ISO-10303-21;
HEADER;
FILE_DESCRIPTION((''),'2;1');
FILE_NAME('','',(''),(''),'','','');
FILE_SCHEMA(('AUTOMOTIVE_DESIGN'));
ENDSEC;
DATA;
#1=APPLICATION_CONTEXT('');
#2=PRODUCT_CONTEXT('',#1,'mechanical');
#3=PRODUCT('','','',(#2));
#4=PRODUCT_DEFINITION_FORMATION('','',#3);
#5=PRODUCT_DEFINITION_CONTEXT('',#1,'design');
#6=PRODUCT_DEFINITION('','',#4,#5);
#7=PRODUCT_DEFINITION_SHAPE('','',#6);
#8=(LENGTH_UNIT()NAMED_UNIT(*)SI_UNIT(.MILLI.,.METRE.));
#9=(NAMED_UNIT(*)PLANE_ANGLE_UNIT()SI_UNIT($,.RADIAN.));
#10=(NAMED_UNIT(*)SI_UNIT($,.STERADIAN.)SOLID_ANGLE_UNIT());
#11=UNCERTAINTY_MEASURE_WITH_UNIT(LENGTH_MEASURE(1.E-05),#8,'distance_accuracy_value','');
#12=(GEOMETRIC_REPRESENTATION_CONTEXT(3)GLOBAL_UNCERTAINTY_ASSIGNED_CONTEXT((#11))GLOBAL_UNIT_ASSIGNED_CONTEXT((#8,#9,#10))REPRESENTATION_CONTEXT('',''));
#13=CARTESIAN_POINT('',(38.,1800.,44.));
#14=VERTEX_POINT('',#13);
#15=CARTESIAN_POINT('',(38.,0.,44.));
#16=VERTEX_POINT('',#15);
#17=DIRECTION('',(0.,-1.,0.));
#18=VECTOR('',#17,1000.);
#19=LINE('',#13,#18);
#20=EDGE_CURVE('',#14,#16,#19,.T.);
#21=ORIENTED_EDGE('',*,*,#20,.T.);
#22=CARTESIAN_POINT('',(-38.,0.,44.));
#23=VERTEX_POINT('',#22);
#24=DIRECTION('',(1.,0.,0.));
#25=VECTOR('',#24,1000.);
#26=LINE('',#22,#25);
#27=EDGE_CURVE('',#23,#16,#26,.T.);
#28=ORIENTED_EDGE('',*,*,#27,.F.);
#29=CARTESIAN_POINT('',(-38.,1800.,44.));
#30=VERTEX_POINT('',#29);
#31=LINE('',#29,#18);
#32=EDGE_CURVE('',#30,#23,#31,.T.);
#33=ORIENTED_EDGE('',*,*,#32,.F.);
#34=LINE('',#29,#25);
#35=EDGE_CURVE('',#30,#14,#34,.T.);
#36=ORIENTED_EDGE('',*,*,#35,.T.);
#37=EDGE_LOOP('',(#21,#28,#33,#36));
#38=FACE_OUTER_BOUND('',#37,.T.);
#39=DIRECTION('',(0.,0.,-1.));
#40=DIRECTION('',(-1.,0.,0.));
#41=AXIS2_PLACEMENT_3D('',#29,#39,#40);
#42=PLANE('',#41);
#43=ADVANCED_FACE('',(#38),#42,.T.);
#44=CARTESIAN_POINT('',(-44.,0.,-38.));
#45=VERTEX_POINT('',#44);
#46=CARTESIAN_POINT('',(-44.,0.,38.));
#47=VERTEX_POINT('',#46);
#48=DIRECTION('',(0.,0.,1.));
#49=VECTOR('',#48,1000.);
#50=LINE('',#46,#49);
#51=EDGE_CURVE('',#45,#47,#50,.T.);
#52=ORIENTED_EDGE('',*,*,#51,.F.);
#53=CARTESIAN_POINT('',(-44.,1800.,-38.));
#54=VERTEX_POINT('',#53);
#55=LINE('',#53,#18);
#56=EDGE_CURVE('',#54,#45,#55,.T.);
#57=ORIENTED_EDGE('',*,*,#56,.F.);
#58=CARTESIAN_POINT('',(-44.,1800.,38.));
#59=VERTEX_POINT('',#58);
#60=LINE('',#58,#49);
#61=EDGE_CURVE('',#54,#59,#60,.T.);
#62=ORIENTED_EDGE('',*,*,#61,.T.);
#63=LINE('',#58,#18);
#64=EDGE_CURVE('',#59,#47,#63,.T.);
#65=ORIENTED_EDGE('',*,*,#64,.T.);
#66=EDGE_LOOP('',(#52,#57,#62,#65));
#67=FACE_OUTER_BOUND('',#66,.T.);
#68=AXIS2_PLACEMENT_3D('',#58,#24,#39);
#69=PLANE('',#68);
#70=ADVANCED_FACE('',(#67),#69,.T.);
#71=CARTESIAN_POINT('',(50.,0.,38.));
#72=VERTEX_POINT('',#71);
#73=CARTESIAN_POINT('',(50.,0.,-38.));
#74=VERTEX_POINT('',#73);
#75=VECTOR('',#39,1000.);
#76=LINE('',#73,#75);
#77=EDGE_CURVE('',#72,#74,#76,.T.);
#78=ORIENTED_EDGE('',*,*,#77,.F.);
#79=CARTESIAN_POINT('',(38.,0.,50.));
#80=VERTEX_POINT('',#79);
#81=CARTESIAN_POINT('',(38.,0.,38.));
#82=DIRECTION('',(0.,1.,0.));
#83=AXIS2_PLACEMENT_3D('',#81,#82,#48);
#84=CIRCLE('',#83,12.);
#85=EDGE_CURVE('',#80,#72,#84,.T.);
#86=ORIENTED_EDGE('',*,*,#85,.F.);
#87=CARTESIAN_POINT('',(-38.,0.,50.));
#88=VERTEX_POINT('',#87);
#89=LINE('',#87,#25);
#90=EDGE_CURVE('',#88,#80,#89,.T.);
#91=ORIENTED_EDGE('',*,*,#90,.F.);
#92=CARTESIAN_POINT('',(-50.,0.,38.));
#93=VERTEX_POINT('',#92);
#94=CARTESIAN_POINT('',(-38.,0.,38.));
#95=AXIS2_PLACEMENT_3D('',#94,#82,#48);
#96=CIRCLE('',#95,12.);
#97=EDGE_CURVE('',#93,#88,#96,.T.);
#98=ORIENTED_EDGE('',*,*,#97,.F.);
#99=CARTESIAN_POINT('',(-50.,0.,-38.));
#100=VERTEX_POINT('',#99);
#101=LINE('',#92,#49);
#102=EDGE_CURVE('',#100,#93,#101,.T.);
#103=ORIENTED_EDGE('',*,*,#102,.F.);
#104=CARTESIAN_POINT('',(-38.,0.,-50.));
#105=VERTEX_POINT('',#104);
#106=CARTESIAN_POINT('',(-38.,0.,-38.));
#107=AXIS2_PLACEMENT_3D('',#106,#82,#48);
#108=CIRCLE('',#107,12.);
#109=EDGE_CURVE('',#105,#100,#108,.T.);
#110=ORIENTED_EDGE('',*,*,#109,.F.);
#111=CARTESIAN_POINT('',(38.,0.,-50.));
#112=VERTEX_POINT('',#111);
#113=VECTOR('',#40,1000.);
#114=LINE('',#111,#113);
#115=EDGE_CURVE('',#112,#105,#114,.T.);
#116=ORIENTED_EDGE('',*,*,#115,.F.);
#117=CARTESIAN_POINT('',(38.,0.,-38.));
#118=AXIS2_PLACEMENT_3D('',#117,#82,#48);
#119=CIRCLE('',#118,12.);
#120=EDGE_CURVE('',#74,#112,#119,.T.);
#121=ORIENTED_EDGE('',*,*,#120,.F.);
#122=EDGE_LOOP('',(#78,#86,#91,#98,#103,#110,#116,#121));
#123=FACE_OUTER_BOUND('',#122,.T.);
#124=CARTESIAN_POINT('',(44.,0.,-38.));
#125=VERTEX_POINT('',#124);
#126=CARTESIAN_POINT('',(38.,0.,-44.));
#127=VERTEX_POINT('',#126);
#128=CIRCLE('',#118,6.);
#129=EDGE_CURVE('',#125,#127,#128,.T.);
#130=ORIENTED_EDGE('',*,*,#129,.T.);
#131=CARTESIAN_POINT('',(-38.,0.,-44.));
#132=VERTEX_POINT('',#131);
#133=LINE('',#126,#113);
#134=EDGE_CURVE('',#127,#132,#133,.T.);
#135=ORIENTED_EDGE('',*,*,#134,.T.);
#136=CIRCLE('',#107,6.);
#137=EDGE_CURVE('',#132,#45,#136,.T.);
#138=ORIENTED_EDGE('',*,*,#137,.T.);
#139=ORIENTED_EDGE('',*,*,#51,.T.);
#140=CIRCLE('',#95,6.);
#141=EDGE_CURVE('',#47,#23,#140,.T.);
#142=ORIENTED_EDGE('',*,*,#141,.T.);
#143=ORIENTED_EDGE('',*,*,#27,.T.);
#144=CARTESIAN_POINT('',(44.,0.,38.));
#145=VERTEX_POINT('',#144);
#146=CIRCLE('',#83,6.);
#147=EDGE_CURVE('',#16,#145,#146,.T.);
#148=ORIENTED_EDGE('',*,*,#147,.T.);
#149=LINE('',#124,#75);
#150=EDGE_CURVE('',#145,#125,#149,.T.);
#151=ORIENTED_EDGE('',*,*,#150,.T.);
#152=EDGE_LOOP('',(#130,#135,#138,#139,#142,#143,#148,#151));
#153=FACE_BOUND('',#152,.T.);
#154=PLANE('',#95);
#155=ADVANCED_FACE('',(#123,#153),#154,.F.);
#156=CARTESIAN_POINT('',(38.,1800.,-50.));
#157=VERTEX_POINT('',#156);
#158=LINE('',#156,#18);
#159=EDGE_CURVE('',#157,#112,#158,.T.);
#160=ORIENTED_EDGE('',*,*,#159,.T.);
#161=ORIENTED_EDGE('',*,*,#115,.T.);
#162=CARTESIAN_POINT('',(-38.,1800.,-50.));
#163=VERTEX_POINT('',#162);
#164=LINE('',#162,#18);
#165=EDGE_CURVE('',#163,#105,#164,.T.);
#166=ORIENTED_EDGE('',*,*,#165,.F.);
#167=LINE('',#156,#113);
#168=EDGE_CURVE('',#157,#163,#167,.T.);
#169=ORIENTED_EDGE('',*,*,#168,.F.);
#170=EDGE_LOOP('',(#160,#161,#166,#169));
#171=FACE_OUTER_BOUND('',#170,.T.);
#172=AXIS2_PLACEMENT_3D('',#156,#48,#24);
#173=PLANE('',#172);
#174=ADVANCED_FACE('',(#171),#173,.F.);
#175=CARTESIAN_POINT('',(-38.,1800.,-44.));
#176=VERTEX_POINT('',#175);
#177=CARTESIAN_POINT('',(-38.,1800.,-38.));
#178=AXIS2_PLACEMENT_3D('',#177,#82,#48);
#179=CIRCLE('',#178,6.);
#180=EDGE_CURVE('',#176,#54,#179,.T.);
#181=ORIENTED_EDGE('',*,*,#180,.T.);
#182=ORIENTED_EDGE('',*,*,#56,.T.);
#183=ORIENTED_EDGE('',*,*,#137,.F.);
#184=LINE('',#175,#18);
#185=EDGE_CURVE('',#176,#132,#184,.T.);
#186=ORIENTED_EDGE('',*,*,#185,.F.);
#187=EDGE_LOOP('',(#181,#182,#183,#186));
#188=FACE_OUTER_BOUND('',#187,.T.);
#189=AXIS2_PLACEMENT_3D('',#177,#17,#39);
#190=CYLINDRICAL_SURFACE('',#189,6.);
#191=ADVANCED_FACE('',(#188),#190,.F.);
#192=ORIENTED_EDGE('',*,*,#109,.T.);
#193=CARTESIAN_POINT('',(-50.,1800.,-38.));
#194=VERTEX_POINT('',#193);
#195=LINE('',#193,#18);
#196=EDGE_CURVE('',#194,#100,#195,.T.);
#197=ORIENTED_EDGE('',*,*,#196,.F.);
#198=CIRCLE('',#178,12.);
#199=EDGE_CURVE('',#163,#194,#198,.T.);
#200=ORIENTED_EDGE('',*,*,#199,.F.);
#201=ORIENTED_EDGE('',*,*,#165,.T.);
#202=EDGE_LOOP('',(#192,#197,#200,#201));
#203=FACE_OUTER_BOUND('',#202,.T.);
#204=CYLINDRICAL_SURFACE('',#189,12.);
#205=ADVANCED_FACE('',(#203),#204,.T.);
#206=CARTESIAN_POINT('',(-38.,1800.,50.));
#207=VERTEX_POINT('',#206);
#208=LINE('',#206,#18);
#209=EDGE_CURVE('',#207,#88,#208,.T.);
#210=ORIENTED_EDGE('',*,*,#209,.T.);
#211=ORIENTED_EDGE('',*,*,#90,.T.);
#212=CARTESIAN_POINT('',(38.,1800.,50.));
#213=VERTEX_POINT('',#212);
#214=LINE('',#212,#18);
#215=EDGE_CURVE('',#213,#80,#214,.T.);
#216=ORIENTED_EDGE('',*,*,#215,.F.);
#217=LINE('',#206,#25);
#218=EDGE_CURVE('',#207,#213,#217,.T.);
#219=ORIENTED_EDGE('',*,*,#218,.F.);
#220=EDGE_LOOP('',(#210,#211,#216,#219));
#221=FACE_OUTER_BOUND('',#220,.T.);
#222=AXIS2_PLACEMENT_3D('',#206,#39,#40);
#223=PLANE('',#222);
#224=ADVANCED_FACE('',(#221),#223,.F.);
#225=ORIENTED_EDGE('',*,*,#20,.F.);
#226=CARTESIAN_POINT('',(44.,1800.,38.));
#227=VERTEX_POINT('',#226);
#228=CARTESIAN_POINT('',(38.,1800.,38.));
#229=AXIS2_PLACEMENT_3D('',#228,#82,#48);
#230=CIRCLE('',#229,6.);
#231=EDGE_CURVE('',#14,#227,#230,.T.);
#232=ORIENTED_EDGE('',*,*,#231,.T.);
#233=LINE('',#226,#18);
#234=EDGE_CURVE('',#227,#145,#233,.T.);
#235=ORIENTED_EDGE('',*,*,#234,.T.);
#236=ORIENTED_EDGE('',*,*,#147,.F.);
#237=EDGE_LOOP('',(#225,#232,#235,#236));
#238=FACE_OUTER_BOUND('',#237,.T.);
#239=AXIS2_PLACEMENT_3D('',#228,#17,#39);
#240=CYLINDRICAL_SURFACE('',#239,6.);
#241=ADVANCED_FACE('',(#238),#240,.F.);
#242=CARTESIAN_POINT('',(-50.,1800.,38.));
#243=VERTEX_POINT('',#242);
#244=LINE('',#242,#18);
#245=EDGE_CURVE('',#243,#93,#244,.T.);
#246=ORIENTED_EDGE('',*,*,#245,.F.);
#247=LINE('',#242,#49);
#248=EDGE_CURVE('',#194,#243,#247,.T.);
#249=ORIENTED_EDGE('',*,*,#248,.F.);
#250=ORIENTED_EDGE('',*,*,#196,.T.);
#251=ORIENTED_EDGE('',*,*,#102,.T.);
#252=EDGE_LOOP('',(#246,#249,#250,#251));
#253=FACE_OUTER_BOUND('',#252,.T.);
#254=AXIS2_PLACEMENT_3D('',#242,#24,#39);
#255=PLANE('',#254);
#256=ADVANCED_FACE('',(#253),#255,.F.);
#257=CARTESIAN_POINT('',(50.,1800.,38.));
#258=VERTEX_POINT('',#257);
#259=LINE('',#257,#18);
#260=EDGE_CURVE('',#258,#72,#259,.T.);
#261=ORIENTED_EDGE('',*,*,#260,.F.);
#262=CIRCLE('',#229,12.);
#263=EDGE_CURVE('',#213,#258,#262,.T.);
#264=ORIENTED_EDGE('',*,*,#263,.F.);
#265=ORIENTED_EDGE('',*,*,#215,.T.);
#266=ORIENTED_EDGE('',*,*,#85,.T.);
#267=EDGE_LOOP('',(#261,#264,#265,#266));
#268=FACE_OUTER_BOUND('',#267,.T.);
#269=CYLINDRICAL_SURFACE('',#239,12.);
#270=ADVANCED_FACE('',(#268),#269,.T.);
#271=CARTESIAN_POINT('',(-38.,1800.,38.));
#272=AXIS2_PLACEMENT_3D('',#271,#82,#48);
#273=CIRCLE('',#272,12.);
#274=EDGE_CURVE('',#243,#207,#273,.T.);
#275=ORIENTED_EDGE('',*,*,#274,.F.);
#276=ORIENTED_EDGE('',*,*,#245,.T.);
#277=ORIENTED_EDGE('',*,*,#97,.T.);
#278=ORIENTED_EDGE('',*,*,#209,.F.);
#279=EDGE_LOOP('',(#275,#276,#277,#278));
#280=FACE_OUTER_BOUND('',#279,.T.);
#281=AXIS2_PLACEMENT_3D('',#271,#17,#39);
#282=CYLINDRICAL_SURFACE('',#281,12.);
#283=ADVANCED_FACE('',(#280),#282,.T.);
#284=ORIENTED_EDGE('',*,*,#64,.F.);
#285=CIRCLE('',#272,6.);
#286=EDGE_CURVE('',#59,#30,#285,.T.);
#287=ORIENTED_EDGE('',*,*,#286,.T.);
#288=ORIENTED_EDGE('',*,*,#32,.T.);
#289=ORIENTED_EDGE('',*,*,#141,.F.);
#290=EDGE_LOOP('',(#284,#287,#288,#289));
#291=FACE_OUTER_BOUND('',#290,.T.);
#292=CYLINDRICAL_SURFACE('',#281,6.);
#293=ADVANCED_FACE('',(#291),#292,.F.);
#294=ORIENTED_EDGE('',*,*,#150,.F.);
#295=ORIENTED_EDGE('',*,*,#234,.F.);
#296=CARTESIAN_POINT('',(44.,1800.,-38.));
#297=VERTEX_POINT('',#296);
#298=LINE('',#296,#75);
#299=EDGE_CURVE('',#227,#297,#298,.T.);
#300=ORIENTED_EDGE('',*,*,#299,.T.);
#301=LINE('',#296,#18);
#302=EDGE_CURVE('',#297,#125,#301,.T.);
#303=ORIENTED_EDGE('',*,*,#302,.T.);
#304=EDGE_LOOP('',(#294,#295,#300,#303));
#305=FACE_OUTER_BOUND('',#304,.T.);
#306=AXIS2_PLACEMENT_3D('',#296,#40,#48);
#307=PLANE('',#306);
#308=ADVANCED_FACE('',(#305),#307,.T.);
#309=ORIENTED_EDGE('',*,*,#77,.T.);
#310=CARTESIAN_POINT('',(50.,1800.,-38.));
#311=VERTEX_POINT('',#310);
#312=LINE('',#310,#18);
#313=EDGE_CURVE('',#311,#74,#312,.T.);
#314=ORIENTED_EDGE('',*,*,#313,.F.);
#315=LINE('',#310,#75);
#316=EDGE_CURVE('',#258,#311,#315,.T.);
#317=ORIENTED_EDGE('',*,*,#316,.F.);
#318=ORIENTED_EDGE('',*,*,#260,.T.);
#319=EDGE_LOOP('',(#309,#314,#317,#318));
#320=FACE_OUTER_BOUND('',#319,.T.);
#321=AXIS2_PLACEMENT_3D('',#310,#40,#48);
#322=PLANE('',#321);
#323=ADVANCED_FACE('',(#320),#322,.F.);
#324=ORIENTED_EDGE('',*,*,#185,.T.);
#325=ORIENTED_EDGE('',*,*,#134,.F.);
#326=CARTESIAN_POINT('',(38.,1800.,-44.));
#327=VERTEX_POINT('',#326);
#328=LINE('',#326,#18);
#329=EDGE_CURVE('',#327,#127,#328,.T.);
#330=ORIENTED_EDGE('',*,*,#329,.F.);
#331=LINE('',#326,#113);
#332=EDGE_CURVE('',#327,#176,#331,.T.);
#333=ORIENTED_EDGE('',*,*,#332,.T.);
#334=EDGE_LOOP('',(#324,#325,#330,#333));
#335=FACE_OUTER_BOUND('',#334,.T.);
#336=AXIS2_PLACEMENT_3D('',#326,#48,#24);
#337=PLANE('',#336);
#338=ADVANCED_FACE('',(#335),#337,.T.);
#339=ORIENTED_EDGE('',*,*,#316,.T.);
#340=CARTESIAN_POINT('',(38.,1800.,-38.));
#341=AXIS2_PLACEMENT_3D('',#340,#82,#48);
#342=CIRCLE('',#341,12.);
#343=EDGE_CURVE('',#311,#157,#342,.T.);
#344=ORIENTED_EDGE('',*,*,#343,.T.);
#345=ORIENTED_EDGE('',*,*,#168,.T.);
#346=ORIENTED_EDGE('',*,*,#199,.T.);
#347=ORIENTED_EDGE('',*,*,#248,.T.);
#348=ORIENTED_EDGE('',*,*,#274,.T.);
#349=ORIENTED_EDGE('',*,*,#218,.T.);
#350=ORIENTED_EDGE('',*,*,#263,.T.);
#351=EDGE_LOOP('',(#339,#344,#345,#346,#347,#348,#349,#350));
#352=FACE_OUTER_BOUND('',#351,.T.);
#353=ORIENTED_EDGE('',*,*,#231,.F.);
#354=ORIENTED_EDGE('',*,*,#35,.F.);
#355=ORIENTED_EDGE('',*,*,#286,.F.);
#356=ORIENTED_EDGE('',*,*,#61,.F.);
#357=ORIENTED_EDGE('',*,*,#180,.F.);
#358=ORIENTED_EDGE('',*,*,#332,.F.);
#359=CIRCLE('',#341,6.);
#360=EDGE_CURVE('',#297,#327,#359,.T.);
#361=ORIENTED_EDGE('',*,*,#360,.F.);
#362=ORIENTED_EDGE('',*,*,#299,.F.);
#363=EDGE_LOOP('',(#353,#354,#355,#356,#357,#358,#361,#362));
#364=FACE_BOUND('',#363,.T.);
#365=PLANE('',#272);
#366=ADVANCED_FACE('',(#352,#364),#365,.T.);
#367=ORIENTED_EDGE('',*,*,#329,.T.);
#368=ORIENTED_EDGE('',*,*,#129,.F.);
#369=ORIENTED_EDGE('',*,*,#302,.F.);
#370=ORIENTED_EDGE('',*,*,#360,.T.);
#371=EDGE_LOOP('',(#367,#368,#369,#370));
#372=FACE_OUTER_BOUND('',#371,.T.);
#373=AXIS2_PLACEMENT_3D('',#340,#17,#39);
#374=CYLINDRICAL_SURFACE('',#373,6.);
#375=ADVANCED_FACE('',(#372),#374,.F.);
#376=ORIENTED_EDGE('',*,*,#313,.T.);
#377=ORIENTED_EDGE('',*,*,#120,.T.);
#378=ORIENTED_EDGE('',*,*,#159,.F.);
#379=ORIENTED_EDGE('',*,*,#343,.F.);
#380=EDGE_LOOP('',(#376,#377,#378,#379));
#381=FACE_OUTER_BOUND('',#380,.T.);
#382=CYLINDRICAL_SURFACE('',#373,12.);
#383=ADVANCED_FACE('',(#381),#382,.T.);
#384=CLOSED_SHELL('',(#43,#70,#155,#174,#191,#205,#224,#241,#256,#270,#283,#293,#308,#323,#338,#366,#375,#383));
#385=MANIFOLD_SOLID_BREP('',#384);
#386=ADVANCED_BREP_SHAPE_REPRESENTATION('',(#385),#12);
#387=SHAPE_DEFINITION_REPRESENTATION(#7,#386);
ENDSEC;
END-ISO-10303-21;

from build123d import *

# Parameters (mm, degrees)
GB_T_6728_2002_SQUARE_HOLLOW_SECTION_100_DEPTH = 1800


with BuildPart() as part:
    # Sketch11 → GB/T 6728-2002 square hollow section 100×100×6(1) (new body)
    with BuildSketch(Plane(origin=(0, 0, 0), x_dir=(-1, 0, 0), z_dir=(0, 1, 0))):
        with BuildLine():
            Line((-38, -50), (38, -50))
            ThreePointArc((38, -50), (46.485281374, -46.485281374), (50, -38))
            Line((50, -38), (50, 38))
            ThreePointArc((50, 38), (46.485281374, 46.485281374), (38, 50))
            Line((38, 50), (-38, 50))
            ThreePointArc((-38, 50), (-46.485281374, 46.485281374), (-50, 38))
            Line((-50, 38), (-50, -38))
            ThreePointArc((-50, -38), (-46.485281374, -46.485281374), (-38, -50))
        make_face()
        with BuildLine():
            Line((-38, -44), (38, -44))
            ThreePointArc((38, -44), (42.242640687, -42.242640687), (44, -38))
            Line((44, -38), (44, 38))
            ThreePointArc((44, 38), (42.242640687, 42.242640687), (38, 44))
            Line((38, 44), (-38, 44))
            ThreePointArc((-38, 44), (-42.242640687, 42.242640687), (-44, 38))
            Line((-44, 38), (-44, -38))
            ThreePointArc((-44, -38), (-42.242640687, -42.242640687), (-38, -44))
        make_face(mode=Mode.SUBTRACT)
    extrude(amount=GB_T_6728_2002_SQUARE_HOLLOW_SECTION_100_DEPTH)


solid = part.part
